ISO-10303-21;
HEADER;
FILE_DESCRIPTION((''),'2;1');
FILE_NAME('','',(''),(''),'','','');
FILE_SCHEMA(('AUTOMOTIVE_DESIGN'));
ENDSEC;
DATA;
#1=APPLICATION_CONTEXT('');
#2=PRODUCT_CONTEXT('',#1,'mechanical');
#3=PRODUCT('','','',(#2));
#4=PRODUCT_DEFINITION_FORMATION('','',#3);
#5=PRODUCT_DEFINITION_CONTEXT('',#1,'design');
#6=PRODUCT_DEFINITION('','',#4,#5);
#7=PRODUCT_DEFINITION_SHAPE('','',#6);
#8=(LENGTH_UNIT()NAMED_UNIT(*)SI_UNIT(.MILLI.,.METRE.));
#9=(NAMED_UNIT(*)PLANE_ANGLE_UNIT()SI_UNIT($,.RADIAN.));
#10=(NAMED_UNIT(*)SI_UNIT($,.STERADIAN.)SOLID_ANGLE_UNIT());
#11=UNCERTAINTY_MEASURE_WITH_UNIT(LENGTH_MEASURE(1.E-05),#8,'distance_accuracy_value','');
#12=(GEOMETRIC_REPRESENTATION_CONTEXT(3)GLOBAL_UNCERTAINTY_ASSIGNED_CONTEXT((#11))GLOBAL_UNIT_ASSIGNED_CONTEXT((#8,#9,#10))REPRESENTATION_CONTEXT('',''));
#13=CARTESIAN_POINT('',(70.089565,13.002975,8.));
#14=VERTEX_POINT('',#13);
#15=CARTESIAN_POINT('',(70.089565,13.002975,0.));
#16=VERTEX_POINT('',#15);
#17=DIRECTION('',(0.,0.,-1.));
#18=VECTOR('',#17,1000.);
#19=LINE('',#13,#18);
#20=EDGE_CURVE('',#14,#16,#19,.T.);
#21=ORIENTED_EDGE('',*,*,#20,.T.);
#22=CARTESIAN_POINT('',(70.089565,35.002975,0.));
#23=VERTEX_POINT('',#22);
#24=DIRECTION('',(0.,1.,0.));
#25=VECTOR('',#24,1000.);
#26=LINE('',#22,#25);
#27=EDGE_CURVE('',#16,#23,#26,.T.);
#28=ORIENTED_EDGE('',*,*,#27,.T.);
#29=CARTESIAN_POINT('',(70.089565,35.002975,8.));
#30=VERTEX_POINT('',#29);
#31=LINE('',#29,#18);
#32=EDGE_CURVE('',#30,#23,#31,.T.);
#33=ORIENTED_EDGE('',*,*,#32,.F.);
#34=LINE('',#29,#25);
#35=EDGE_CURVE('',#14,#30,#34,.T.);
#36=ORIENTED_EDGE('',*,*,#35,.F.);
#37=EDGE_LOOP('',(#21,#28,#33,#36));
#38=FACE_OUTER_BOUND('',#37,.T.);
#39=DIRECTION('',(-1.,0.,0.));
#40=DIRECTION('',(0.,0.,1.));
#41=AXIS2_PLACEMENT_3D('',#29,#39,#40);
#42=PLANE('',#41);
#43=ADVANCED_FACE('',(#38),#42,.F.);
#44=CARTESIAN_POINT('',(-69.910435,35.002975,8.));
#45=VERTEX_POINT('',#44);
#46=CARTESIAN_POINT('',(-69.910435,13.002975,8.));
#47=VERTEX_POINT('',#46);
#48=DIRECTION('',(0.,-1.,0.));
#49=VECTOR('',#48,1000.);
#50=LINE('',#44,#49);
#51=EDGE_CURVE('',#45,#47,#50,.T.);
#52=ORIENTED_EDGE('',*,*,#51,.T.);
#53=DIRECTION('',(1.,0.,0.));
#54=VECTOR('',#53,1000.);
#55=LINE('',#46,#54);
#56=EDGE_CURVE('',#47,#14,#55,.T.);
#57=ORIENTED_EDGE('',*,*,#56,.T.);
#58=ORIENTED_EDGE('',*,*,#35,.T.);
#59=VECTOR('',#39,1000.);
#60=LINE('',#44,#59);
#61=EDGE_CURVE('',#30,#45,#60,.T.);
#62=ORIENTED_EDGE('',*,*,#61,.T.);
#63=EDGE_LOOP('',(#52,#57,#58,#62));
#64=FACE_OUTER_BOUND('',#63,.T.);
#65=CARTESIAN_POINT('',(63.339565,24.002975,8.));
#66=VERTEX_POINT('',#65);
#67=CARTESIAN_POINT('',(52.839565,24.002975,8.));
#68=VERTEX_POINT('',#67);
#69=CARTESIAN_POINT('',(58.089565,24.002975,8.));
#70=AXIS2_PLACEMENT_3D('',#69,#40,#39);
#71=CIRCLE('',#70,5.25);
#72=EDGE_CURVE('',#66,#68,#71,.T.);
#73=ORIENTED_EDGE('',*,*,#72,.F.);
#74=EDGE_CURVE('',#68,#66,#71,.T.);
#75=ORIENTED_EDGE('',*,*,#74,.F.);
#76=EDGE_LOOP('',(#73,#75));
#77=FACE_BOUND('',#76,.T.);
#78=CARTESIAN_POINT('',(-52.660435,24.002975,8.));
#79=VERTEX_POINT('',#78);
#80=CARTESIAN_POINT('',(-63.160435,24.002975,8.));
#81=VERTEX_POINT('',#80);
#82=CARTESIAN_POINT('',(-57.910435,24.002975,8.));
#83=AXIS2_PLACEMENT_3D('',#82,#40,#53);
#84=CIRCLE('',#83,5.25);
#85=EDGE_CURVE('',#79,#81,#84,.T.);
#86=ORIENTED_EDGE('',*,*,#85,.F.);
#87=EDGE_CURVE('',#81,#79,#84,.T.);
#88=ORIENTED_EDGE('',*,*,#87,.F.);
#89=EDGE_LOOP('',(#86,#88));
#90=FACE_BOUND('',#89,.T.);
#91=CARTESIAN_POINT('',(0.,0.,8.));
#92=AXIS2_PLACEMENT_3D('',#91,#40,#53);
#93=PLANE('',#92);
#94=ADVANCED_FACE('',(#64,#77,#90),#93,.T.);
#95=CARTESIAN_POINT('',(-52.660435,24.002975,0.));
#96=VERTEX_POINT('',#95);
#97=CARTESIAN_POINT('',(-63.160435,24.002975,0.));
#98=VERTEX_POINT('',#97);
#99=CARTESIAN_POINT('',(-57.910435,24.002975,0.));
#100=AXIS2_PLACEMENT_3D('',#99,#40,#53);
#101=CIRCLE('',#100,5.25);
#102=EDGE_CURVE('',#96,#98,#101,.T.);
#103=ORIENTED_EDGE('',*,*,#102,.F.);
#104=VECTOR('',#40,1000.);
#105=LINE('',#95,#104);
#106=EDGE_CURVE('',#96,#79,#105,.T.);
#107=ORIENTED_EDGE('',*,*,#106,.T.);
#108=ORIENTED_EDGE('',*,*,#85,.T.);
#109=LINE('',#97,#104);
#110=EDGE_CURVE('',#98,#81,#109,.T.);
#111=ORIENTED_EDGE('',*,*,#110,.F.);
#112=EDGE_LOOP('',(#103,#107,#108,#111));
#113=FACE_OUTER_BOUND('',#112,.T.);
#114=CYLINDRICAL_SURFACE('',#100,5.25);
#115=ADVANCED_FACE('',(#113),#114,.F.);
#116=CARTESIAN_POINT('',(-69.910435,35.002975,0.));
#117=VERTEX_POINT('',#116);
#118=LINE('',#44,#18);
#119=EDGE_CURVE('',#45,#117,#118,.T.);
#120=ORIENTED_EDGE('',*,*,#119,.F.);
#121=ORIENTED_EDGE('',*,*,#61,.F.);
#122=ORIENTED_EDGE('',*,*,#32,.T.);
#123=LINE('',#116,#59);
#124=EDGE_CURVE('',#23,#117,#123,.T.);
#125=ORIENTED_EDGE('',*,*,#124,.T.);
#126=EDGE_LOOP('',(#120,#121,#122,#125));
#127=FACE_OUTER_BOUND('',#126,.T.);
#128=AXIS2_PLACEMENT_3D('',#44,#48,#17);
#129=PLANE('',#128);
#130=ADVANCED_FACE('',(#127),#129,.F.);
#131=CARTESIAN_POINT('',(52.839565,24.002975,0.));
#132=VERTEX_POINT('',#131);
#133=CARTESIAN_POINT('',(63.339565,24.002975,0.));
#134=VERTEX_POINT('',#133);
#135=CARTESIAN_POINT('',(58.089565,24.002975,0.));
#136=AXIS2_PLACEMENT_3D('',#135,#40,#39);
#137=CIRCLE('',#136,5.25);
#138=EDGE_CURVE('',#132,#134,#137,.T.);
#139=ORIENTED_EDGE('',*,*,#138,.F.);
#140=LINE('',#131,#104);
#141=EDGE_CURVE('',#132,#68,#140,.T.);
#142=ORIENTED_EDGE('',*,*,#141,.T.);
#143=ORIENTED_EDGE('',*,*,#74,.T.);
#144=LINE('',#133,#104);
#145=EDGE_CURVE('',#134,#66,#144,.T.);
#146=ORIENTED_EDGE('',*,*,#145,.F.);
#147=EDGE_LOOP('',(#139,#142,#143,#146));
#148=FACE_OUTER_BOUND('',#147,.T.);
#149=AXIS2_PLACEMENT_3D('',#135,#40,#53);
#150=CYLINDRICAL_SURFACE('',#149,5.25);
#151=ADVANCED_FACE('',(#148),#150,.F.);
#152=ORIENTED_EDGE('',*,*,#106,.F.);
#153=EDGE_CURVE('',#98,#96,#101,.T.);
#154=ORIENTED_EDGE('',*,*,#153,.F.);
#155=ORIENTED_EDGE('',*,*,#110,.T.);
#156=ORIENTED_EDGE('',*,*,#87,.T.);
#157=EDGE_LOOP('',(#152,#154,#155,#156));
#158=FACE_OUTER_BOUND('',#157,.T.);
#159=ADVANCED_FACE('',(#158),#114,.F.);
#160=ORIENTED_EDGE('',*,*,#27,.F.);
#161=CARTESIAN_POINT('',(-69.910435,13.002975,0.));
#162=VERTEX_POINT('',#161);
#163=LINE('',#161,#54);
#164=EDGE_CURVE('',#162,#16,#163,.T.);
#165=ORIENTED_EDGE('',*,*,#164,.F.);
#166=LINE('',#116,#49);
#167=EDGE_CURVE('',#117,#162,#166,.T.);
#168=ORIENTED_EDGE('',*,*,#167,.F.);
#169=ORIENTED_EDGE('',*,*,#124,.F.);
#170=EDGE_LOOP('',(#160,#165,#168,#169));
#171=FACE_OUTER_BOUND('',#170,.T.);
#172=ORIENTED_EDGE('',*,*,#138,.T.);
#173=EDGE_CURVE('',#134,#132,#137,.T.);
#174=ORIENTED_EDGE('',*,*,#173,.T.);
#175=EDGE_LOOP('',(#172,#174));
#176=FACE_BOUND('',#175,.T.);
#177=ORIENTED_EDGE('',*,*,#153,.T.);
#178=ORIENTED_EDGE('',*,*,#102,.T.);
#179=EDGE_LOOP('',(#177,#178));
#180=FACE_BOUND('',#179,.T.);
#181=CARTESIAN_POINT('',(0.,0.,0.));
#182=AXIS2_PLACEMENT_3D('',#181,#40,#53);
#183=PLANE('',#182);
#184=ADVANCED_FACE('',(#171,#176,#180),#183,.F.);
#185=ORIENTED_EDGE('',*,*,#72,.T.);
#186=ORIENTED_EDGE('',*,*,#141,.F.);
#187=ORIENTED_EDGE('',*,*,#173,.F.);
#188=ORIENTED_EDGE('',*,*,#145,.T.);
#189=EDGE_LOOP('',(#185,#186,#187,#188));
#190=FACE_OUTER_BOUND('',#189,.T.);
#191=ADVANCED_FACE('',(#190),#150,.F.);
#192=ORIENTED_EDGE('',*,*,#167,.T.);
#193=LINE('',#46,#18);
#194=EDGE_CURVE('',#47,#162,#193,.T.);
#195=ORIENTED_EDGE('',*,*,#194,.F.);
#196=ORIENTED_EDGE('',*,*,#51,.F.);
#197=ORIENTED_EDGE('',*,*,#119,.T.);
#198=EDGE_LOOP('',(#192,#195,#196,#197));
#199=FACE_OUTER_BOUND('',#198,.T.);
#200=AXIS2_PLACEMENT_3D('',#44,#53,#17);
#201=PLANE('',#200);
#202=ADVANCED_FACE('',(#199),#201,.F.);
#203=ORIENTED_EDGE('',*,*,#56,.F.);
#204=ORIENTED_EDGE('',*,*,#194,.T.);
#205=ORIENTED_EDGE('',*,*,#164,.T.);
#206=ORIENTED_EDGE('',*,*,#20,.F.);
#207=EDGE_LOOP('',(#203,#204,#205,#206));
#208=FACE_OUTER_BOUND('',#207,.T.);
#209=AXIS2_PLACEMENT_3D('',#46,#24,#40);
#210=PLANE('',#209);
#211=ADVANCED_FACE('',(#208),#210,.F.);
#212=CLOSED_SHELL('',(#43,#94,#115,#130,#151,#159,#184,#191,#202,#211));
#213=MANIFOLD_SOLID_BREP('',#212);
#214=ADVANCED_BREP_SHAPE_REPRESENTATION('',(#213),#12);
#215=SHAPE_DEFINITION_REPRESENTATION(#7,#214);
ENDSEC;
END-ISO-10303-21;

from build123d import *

# Parameters (mm, degrees)
SKETCH1_W           = 140
SKETCH1_H           = 22
BOSS_EXTRUDE1_DEPTH = 8
SKETCH2_R           = 5.25
CUT_EXTRUDE1_DEPTH  = 79.751224998


with BuildPart() as part:
    # Sketch1 → Boss-Extrude1 (new body)
    with BuildSketch(Plane.XY):
        with Locations((0.089565278, 24.00297527)):
            Rectangle(SKETCH1_W, SKETCH1_H)
    extrude(amount=BOSS_EXTRUDE1_DEPTH)

    # Sketch2 → Cut-Extrude1 (cut, through all)
    with BuildSketch(Plane.XY.offset(8)):
        with Locations((-57.910434722, 24.00297527)):
            Circle(SKETCH2_R)
        with Locations(Location((58.089565278, 24.00297527, 0), (0, 0, 180))):
            Circle(SKETCH2_R)
    extrude(amount=-CUT_EXTRUDE1_DEPTH, mode=Mode.SUBTRACT)


solid = part.part
